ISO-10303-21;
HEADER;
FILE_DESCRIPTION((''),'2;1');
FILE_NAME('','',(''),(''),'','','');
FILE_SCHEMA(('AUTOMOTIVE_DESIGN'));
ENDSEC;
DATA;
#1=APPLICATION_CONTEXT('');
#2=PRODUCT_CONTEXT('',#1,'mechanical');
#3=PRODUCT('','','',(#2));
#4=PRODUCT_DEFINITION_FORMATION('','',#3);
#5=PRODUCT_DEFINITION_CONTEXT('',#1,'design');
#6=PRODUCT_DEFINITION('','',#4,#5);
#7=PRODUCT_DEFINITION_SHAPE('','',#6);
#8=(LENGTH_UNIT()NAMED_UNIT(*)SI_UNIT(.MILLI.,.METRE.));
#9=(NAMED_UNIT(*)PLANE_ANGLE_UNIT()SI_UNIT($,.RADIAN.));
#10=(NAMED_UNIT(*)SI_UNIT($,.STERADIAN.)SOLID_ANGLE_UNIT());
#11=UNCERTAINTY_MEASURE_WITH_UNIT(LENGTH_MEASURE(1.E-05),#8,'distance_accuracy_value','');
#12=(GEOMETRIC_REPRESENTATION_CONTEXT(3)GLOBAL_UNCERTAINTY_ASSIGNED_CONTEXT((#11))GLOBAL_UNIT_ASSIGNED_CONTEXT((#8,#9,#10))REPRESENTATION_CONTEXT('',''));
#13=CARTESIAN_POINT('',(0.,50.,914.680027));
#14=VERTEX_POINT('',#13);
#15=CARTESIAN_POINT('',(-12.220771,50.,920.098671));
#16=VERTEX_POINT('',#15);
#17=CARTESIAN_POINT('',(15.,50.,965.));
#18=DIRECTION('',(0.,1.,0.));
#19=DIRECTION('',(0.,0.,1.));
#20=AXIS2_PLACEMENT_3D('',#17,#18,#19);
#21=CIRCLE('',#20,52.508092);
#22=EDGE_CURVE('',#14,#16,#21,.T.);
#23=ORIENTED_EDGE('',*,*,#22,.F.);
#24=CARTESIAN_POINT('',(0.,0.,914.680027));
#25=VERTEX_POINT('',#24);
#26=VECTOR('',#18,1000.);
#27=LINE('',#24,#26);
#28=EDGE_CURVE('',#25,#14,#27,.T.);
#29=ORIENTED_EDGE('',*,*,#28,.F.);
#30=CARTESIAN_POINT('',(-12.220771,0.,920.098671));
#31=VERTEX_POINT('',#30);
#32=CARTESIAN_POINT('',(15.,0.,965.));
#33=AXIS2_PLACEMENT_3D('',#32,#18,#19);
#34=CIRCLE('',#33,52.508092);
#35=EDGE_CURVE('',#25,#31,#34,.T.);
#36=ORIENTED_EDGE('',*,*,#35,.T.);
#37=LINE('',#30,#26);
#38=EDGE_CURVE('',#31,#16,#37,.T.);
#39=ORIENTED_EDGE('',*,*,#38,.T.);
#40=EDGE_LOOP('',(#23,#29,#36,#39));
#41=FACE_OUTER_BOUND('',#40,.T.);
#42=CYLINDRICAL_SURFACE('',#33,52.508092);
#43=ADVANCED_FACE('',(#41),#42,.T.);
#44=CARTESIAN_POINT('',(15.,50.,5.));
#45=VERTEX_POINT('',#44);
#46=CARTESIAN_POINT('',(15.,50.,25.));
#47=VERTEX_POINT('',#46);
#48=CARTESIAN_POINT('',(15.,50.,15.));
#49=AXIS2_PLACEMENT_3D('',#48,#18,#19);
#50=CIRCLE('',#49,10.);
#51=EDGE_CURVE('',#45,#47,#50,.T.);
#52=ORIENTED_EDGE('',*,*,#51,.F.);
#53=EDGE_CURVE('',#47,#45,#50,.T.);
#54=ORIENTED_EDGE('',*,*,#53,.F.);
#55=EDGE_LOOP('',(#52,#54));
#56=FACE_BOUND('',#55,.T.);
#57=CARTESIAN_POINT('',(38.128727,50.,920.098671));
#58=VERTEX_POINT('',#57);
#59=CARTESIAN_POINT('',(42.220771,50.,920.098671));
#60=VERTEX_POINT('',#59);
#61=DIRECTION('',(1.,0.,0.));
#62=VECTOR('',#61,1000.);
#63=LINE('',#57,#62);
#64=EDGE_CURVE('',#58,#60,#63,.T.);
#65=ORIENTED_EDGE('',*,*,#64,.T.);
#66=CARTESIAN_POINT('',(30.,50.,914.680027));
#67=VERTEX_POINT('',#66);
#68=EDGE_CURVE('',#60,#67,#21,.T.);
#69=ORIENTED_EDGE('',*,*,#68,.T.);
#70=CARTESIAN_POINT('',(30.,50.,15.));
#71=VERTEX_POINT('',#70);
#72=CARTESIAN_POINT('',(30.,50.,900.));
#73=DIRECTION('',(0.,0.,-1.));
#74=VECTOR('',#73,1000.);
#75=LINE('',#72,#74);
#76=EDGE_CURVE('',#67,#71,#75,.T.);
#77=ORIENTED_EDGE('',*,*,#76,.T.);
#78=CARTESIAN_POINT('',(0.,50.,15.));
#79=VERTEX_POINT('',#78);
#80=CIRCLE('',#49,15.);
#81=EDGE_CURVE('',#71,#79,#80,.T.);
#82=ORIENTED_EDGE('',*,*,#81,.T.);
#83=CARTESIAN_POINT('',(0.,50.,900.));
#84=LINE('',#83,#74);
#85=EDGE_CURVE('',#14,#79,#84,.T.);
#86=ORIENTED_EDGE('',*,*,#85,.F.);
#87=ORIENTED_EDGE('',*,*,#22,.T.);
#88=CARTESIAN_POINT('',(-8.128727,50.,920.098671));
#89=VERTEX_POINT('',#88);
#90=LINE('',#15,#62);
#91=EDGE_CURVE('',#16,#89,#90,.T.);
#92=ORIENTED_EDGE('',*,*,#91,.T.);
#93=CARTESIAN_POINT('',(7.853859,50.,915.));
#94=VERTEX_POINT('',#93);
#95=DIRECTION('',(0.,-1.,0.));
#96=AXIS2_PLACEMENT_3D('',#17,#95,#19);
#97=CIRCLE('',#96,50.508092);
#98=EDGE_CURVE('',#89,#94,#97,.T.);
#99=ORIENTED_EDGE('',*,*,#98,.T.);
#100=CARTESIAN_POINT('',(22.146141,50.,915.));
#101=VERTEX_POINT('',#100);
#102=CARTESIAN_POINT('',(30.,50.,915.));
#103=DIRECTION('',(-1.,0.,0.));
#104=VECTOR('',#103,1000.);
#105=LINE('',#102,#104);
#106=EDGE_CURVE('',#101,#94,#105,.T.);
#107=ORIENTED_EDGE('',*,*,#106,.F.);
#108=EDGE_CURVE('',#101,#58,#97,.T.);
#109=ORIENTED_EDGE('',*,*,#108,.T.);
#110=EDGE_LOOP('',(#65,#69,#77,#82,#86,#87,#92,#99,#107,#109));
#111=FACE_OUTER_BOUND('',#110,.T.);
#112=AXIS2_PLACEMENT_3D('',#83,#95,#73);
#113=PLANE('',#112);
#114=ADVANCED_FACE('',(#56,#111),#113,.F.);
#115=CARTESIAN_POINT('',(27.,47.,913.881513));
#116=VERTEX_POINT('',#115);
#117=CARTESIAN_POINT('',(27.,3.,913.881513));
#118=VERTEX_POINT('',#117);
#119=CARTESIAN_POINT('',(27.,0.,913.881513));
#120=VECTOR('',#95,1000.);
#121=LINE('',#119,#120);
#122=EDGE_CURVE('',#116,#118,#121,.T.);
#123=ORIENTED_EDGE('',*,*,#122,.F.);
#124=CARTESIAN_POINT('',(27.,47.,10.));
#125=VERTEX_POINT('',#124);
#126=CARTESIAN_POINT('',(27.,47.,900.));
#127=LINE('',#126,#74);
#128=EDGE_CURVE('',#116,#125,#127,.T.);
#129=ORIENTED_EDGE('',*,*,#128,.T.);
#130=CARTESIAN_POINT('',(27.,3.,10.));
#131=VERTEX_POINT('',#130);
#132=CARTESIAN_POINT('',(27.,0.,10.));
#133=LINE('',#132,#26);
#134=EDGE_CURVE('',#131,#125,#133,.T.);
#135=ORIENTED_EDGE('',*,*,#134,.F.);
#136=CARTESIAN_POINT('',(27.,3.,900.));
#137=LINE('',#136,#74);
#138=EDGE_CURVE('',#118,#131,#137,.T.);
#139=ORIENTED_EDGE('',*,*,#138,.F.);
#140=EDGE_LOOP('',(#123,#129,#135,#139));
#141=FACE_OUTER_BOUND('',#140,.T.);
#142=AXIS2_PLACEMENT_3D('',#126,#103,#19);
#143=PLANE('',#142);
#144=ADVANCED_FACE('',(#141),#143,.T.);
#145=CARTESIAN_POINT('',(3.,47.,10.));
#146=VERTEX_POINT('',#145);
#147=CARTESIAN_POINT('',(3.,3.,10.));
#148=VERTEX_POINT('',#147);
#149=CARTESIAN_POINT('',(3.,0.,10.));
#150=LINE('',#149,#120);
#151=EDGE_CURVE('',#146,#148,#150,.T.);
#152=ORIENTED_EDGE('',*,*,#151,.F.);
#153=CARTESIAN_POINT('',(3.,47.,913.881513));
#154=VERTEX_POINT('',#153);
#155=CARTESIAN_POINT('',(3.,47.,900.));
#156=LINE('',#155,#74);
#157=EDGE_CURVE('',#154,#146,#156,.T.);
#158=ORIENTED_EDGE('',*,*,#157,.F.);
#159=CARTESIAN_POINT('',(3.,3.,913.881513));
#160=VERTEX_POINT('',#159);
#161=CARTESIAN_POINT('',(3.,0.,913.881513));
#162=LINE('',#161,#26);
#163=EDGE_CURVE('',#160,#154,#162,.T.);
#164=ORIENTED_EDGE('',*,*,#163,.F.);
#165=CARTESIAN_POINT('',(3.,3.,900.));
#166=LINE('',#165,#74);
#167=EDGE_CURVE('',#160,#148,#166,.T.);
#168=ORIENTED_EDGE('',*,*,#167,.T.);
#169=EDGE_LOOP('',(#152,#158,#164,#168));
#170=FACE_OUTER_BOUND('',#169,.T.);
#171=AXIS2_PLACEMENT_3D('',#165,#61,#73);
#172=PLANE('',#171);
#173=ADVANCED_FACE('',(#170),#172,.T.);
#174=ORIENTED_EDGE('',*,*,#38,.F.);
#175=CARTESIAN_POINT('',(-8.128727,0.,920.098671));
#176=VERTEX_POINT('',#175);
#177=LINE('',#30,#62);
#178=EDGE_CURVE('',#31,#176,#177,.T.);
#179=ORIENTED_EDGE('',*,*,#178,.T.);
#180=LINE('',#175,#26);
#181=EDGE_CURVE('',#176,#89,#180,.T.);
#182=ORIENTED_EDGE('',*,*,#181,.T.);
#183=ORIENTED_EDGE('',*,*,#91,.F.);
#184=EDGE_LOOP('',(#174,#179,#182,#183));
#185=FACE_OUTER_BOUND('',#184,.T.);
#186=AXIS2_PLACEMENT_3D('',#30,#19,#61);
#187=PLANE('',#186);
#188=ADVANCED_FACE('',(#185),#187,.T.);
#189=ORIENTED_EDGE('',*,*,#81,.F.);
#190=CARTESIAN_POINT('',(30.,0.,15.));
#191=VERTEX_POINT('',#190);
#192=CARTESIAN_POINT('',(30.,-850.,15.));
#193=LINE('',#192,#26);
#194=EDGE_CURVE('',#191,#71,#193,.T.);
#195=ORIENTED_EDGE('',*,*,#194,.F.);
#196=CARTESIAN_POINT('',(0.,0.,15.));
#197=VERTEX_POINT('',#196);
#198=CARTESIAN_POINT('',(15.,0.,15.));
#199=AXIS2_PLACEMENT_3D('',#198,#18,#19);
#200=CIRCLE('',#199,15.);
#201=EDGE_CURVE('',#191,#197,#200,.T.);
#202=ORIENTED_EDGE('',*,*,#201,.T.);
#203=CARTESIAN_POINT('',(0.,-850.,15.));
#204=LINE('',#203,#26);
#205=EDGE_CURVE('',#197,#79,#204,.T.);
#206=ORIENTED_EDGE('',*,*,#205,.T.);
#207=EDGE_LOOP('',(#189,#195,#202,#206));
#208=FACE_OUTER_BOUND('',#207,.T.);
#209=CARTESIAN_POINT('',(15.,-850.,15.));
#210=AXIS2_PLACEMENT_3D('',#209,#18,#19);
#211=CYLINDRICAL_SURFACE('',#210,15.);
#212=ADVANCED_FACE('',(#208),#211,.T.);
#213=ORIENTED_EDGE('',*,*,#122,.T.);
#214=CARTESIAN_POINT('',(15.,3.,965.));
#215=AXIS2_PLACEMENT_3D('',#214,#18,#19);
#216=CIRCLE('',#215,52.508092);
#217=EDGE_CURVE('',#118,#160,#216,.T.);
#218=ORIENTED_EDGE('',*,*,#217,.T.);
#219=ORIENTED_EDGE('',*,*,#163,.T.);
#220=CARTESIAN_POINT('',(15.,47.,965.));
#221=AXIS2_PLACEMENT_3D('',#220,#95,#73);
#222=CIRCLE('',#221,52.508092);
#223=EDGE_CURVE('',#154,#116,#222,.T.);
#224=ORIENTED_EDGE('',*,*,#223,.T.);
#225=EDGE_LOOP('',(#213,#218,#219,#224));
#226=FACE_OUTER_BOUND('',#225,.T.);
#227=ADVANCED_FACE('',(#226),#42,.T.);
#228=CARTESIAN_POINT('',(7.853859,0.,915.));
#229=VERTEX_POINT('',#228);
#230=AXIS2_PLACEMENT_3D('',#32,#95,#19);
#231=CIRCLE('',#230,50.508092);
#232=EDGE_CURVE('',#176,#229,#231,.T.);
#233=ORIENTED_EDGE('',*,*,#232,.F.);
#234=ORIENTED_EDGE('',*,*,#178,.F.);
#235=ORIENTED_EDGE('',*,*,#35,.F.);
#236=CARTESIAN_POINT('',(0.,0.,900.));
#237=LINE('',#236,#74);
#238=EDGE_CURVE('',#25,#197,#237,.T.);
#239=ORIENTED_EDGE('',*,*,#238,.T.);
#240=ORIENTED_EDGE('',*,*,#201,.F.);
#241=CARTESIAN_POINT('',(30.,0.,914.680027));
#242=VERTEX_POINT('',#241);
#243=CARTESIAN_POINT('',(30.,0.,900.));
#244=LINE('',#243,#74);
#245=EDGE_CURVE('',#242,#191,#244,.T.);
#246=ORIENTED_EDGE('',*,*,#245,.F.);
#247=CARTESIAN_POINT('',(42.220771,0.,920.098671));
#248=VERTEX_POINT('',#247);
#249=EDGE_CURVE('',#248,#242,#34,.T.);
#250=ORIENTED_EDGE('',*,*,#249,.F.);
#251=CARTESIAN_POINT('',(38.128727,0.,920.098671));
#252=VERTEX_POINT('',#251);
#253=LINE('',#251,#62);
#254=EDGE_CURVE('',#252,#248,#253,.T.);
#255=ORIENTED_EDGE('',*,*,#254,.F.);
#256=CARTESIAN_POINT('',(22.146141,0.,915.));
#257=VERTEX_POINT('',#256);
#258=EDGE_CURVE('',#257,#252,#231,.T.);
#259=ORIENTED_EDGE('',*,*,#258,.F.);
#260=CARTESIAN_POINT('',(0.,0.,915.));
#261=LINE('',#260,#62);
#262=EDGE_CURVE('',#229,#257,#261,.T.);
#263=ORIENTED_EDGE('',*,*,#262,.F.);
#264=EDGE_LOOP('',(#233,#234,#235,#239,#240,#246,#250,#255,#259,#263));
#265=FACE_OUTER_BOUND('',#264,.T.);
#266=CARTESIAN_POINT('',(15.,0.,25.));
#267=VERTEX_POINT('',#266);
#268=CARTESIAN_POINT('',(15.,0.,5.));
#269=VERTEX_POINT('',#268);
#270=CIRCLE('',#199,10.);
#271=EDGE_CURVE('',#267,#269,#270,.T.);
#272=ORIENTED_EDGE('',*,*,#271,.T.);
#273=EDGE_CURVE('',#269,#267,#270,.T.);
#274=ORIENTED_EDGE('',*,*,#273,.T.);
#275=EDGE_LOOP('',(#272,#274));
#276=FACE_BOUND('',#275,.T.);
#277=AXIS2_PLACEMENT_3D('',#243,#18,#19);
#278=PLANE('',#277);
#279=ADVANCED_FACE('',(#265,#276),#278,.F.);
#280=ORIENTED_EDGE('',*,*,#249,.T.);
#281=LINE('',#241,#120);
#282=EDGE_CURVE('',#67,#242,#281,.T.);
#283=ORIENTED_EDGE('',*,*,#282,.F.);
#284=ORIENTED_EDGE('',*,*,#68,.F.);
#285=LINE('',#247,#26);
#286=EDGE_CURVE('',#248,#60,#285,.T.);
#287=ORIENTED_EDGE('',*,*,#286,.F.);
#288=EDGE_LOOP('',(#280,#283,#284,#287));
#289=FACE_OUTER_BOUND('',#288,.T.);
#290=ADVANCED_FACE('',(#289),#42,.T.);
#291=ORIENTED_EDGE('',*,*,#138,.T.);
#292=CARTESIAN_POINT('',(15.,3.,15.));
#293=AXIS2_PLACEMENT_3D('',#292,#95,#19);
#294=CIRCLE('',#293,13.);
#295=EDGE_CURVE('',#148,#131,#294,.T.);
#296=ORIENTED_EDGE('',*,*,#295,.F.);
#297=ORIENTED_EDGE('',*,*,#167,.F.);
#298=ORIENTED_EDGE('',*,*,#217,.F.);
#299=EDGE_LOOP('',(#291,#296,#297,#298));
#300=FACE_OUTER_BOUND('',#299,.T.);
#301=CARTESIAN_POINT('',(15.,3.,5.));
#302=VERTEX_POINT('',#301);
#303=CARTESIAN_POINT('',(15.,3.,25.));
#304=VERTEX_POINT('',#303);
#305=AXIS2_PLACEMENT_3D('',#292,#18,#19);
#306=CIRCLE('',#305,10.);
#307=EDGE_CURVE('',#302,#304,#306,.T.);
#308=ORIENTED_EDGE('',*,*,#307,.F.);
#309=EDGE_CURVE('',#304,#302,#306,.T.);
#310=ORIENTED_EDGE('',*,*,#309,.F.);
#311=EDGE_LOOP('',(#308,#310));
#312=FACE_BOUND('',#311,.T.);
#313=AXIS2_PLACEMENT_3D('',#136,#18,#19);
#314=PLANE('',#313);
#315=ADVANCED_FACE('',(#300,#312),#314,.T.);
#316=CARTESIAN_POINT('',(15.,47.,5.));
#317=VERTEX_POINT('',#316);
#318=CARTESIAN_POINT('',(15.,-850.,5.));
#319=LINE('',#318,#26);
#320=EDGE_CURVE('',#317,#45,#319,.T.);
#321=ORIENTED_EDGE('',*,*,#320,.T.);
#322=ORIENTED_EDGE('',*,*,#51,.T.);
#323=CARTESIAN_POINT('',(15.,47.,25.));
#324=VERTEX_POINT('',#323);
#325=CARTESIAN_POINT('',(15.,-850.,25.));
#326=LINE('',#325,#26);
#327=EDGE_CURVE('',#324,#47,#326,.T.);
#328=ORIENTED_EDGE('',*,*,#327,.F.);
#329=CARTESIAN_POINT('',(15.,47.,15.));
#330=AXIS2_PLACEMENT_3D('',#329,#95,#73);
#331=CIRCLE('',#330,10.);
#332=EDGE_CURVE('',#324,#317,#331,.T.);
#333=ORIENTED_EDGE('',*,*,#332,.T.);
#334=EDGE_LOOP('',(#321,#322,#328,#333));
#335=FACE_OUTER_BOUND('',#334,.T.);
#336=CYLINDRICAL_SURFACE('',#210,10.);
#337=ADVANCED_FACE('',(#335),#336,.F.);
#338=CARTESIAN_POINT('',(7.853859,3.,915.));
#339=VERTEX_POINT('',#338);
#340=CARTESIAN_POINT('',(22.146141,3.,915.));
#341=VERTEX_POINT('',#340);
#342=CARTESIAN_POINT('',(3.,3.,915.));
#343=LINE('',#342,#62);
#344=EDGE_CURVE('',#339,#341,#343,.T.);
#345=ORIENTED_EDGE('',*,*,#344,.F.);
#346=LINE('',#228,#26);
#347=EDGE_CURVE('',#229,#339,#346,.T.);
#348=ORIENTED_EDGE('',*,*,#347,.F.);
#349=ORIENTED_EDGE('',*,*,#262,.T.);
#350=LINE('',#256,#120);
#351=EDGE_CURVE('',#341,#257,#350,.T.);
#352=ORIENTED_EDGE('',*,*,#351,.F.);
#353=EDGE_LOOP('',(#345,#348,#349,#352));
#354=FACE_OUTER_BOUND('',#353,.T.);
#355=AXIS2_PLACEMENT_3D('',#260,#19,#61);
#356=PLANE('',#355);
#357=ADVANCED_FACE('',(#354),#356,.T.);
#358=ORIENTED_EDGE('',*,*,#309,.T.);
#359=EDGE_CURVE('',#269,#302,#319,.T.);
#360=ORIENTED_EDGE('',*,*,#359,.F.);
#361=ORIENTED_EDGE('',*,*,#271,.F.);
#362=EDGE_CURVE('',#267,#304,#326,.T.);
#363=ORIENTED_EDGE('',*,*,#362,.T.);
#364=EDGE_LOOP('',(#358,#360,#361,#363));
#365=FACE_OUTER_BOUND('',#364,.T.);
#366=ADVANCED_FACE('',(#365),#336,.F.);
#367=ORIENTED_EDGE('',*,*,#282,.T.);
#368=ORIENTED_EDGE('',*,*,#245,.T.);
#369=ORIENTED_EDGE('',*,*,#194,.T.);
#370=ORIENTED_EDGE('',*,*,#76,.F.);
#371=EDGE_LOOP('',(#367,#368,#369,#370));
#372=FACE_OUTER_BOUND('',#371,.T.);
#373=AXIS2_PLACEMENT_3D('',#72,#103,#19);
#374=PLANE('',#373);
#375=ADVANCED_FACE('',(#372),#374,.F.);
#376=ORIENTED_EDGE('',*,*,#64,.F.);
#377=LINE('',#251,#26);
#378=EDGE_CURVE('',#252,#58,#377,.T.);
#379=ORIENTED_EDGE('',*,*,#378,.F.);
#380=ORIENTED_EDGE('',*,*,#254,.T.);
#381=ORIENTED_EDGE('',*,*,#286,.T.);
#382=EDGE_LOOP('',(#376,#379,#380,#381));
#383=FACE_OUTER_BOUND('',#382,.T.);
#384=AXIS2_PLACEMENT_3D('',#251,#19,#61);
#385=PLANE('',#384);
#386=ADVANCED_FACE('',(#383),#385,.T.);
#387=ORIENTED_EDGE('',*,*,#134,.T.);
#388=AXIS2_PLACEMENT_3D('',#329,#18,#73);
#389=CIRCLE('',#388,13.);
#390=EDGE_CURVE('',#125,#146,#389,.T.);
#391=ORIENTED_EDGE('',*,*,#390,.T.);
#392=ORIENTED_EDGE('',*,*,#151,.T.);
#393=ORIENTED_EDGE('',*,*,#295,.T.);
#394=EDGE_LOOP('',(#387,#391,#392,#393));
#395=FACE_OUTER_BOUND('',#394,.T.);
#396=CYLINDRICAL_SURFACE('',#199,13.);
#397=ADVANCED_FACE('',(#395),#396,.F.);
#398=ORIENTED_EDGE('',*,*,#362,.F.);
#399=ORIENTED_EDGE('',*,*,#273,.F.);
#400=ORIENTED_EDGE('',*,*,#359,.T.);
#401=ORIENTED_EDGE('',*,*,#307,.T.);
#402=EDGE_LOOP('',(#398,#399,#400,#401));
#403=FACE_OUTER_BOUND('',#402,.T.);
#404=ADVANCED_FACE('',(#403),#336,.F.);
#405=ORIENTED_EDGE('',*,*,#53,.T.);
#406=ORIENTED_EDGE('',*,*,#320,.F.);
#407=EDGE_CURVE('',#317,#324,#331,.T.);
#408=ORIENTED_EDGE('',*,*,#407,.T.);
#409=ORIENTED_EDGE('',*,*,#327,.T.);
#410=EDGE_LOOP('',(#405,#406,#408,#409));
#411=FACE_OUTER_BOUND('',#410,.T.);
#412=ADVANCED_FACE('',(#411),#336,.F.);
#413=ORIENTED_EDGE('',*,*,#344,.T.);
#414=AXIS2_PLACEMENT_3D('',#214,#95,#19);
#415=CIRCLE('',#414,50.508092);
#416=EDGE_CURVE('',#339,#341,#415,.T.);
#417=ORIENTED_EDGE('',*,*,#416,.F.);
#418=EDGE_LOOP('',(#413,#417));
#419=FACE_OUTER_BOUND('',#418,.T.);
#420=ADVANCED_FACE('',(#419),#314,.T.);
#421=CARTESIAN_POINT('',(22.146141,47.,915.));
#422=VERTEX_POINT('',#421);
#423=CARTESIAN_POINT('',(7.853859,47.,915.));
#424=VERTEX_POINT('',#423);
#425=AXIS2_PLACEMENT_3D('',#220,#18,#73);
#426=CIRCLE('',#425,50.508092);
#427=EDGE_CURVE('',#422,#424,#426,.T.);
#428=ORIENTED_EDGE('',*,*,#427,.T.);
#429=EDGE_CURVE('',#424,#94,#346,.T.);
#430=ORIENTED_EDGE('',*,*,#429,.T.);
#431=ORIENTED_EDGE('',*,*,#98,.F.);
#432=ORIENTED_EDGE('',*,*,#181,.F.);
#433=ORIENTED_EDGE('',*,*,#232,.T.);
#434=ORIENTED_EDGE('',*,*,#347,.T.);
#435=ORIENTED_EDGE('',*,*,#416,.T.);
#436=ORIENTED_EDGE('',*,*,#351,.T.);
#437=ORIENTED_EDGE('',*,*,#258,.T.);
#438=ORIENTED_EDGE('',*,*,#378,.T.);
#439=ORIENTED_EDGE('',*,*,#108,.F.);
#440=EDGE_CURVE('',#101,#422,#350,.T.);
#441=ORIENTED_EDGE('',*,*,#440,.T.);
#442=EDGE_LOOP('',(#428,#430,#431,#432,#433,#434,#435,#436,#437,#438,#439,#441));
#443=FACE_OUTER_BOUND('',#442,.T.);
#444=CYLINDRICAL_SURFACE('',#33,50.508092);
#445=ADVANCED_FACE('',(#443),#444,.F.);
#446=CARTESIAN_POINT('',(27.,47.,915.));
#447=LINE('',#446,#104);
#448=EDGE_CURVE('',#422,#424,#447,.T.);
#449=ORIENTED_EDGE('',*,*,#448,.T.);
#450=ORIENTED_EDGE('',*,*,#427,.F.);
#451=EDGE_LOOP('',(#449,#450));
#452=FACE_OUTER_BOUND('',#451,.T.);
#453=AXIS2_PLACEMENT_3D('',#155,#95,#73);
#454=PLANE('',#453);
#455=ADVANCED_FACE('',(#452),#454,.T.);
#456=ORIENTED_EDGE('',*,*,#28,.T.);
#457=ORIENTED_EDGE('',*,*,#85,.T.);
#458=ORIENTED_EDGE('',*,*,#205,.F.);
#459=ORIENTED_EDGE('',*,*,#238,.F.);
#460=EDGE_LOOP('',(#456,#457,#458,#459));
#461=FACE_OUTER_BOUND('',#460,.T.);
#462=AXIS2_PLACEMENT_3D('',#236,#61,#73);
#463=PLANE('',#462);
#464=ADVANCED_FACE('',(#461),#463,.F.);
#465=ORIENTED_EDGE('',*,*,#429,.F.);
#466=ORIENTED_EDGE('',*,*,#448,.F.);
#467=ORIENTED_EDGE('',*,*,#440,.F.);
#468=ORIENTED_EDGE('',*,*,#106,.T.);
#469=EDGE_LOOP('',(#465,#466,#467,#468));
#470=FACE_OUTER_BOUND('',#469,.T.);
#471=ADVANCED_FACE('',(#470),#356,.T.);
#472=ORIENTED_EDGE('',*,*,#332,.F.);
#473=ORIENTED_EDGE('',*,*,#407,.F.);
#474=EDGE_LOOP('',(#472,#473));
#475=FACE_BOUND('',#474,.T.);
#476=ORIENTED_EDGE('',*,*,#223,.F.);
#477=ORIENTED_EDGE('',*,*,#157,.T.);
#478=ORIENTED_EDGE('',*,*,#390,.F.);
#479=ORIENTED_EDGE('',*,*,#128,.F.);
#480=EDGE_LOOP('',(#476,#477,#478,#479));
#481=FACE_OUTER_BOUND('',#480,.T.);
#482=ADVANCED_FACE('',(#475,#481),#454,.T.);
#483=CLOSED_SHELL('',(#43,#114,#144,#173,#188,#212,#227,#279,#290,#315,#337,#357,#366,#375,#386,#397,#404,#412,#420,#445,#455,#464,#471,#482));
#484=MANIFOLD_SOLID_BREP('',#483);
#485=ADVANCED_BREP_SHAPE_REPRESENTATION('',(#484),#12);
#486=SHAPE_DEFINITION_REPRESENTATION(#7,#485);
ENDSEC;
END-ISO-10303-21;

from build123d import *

# Parameters (mm, degrees)
SKETCH_1_W          = 30
SKETCH_1_H          = 50
SKETCH_1_W_2        = 24
SKETCH_1_H_2        = 44
EXTRUDE_1_DEPTH     = 900
SKETCH_2_R          = 10
CUT_EXTRUDE_2_DEPTH = 900
EXTRUDE_2_DEPTH     = 50
SKETCH_4_W          = 30
SKETCH_4_H          = 50
SKETCH_4_W_2        = 24
SKETCH_4_H_2        = 44
EXTRUDE_3_DEPTH     = 15
EXTRUDE_4_DEPTH     = 50


with BuildPart() as part:
    # 草图1 → 凸台-拉伸1 (new body)
    with BuildSketch(Plane.XY):
        with Locations((15, 25)):
            Rectangle(SKETCH_1_W, SKETCH_1_H)
        with Locations((15, 25)):
            Rectangle(SKETCH_1_W_2, SKETCH_1_H_2, mode=Mode.SUBTRACT)
    extrude(amount=EXTRUDE_1_DEPTH)

    # 草图2 → 切除-拉伸2 (cut)
    with BuildSketch(Plane(origin=(0, 50, 0), x_dir=(1, 0, 0), z_dir=(0, 1, 0))):
        with Locations(Location((15, -15, 0), (0, 0, 270))):
            Circle(SKETCH_2_R)
        with BuildLine():
            ThreePointArc((0, -15), (4.393398282, -4.393398282), (15, 0))
            Line((15, 0), (0, 0))
            Line((0, 0), (0, -15))
        make_face()
        with BuildLine():
            Line((30, 0), (15, 0))
            ThreePointArc((15, 0), (25.606601718, -4.393398282), (30, -15))
            Line((30, -15), (30, 0))
        make_face()
    extrude(amount=-CUT_EXTRUDE_2_DEPTH, mode=Mode.SUBTRACT)

    # 草图3 → 凸台-拉伸2 (add)
    with BuildSketch(Plane(origin=(0, 50, 0), x_dir=(1, 0, 0), z_dir=(0, 1, 0))):
        with BuildLine():
            Line((2, -15), (0, -15))
            ThreePointArc((0, -15), (15, 0), (30, -15))
            Line((30, -15), (28, -15))
            ThreePointArc((28, -15), (15, -2), (2, -15))
        make_face()
    extrude(amount=-EXTRUDE_2_DEPTH)

    # 草图4 → 凸台-拉伸3 (add)
    with BuildSketch(Plane.XY.offset(900)):
        with Locations((15, 25)):
            Rectangle(SKETCH_4_W, SKETCH_4_H)
        with Locations((15, 25)):
            Rectangle(SKETCH_4_W_2, SKETCH_4_H_2, mode=Mode.SUBTRACT)
    extrude(amount=EXTRUDE_3_DEPTH)

    # 草图5 → 凸台-拉伸4 (add)
    with BuildSketch(Plane(origin=(0, 50, 0), x_dir=(1, 0, 0), z_dir=(0, 1, 0))):
        with BuildLine():
            Line((-12.2207709, -920.098671199), (-8.128726759, -920.098671199))
            ThreePointArc((-8.128726759, -920.098671199), (15, -914.491908276), (38.128726759, -920.098671199))
            Line((38.128726759, -920.098671199), (42.2207709, -920.098671199))
            ThreePointArc((42.2207709, -920.098671199), (15, -912.491908276), (-12.2207709, -920.098671199))
        make_face()
    extrude(amount=-EXTRUDE_4_DEPTH)


solid = part.part
